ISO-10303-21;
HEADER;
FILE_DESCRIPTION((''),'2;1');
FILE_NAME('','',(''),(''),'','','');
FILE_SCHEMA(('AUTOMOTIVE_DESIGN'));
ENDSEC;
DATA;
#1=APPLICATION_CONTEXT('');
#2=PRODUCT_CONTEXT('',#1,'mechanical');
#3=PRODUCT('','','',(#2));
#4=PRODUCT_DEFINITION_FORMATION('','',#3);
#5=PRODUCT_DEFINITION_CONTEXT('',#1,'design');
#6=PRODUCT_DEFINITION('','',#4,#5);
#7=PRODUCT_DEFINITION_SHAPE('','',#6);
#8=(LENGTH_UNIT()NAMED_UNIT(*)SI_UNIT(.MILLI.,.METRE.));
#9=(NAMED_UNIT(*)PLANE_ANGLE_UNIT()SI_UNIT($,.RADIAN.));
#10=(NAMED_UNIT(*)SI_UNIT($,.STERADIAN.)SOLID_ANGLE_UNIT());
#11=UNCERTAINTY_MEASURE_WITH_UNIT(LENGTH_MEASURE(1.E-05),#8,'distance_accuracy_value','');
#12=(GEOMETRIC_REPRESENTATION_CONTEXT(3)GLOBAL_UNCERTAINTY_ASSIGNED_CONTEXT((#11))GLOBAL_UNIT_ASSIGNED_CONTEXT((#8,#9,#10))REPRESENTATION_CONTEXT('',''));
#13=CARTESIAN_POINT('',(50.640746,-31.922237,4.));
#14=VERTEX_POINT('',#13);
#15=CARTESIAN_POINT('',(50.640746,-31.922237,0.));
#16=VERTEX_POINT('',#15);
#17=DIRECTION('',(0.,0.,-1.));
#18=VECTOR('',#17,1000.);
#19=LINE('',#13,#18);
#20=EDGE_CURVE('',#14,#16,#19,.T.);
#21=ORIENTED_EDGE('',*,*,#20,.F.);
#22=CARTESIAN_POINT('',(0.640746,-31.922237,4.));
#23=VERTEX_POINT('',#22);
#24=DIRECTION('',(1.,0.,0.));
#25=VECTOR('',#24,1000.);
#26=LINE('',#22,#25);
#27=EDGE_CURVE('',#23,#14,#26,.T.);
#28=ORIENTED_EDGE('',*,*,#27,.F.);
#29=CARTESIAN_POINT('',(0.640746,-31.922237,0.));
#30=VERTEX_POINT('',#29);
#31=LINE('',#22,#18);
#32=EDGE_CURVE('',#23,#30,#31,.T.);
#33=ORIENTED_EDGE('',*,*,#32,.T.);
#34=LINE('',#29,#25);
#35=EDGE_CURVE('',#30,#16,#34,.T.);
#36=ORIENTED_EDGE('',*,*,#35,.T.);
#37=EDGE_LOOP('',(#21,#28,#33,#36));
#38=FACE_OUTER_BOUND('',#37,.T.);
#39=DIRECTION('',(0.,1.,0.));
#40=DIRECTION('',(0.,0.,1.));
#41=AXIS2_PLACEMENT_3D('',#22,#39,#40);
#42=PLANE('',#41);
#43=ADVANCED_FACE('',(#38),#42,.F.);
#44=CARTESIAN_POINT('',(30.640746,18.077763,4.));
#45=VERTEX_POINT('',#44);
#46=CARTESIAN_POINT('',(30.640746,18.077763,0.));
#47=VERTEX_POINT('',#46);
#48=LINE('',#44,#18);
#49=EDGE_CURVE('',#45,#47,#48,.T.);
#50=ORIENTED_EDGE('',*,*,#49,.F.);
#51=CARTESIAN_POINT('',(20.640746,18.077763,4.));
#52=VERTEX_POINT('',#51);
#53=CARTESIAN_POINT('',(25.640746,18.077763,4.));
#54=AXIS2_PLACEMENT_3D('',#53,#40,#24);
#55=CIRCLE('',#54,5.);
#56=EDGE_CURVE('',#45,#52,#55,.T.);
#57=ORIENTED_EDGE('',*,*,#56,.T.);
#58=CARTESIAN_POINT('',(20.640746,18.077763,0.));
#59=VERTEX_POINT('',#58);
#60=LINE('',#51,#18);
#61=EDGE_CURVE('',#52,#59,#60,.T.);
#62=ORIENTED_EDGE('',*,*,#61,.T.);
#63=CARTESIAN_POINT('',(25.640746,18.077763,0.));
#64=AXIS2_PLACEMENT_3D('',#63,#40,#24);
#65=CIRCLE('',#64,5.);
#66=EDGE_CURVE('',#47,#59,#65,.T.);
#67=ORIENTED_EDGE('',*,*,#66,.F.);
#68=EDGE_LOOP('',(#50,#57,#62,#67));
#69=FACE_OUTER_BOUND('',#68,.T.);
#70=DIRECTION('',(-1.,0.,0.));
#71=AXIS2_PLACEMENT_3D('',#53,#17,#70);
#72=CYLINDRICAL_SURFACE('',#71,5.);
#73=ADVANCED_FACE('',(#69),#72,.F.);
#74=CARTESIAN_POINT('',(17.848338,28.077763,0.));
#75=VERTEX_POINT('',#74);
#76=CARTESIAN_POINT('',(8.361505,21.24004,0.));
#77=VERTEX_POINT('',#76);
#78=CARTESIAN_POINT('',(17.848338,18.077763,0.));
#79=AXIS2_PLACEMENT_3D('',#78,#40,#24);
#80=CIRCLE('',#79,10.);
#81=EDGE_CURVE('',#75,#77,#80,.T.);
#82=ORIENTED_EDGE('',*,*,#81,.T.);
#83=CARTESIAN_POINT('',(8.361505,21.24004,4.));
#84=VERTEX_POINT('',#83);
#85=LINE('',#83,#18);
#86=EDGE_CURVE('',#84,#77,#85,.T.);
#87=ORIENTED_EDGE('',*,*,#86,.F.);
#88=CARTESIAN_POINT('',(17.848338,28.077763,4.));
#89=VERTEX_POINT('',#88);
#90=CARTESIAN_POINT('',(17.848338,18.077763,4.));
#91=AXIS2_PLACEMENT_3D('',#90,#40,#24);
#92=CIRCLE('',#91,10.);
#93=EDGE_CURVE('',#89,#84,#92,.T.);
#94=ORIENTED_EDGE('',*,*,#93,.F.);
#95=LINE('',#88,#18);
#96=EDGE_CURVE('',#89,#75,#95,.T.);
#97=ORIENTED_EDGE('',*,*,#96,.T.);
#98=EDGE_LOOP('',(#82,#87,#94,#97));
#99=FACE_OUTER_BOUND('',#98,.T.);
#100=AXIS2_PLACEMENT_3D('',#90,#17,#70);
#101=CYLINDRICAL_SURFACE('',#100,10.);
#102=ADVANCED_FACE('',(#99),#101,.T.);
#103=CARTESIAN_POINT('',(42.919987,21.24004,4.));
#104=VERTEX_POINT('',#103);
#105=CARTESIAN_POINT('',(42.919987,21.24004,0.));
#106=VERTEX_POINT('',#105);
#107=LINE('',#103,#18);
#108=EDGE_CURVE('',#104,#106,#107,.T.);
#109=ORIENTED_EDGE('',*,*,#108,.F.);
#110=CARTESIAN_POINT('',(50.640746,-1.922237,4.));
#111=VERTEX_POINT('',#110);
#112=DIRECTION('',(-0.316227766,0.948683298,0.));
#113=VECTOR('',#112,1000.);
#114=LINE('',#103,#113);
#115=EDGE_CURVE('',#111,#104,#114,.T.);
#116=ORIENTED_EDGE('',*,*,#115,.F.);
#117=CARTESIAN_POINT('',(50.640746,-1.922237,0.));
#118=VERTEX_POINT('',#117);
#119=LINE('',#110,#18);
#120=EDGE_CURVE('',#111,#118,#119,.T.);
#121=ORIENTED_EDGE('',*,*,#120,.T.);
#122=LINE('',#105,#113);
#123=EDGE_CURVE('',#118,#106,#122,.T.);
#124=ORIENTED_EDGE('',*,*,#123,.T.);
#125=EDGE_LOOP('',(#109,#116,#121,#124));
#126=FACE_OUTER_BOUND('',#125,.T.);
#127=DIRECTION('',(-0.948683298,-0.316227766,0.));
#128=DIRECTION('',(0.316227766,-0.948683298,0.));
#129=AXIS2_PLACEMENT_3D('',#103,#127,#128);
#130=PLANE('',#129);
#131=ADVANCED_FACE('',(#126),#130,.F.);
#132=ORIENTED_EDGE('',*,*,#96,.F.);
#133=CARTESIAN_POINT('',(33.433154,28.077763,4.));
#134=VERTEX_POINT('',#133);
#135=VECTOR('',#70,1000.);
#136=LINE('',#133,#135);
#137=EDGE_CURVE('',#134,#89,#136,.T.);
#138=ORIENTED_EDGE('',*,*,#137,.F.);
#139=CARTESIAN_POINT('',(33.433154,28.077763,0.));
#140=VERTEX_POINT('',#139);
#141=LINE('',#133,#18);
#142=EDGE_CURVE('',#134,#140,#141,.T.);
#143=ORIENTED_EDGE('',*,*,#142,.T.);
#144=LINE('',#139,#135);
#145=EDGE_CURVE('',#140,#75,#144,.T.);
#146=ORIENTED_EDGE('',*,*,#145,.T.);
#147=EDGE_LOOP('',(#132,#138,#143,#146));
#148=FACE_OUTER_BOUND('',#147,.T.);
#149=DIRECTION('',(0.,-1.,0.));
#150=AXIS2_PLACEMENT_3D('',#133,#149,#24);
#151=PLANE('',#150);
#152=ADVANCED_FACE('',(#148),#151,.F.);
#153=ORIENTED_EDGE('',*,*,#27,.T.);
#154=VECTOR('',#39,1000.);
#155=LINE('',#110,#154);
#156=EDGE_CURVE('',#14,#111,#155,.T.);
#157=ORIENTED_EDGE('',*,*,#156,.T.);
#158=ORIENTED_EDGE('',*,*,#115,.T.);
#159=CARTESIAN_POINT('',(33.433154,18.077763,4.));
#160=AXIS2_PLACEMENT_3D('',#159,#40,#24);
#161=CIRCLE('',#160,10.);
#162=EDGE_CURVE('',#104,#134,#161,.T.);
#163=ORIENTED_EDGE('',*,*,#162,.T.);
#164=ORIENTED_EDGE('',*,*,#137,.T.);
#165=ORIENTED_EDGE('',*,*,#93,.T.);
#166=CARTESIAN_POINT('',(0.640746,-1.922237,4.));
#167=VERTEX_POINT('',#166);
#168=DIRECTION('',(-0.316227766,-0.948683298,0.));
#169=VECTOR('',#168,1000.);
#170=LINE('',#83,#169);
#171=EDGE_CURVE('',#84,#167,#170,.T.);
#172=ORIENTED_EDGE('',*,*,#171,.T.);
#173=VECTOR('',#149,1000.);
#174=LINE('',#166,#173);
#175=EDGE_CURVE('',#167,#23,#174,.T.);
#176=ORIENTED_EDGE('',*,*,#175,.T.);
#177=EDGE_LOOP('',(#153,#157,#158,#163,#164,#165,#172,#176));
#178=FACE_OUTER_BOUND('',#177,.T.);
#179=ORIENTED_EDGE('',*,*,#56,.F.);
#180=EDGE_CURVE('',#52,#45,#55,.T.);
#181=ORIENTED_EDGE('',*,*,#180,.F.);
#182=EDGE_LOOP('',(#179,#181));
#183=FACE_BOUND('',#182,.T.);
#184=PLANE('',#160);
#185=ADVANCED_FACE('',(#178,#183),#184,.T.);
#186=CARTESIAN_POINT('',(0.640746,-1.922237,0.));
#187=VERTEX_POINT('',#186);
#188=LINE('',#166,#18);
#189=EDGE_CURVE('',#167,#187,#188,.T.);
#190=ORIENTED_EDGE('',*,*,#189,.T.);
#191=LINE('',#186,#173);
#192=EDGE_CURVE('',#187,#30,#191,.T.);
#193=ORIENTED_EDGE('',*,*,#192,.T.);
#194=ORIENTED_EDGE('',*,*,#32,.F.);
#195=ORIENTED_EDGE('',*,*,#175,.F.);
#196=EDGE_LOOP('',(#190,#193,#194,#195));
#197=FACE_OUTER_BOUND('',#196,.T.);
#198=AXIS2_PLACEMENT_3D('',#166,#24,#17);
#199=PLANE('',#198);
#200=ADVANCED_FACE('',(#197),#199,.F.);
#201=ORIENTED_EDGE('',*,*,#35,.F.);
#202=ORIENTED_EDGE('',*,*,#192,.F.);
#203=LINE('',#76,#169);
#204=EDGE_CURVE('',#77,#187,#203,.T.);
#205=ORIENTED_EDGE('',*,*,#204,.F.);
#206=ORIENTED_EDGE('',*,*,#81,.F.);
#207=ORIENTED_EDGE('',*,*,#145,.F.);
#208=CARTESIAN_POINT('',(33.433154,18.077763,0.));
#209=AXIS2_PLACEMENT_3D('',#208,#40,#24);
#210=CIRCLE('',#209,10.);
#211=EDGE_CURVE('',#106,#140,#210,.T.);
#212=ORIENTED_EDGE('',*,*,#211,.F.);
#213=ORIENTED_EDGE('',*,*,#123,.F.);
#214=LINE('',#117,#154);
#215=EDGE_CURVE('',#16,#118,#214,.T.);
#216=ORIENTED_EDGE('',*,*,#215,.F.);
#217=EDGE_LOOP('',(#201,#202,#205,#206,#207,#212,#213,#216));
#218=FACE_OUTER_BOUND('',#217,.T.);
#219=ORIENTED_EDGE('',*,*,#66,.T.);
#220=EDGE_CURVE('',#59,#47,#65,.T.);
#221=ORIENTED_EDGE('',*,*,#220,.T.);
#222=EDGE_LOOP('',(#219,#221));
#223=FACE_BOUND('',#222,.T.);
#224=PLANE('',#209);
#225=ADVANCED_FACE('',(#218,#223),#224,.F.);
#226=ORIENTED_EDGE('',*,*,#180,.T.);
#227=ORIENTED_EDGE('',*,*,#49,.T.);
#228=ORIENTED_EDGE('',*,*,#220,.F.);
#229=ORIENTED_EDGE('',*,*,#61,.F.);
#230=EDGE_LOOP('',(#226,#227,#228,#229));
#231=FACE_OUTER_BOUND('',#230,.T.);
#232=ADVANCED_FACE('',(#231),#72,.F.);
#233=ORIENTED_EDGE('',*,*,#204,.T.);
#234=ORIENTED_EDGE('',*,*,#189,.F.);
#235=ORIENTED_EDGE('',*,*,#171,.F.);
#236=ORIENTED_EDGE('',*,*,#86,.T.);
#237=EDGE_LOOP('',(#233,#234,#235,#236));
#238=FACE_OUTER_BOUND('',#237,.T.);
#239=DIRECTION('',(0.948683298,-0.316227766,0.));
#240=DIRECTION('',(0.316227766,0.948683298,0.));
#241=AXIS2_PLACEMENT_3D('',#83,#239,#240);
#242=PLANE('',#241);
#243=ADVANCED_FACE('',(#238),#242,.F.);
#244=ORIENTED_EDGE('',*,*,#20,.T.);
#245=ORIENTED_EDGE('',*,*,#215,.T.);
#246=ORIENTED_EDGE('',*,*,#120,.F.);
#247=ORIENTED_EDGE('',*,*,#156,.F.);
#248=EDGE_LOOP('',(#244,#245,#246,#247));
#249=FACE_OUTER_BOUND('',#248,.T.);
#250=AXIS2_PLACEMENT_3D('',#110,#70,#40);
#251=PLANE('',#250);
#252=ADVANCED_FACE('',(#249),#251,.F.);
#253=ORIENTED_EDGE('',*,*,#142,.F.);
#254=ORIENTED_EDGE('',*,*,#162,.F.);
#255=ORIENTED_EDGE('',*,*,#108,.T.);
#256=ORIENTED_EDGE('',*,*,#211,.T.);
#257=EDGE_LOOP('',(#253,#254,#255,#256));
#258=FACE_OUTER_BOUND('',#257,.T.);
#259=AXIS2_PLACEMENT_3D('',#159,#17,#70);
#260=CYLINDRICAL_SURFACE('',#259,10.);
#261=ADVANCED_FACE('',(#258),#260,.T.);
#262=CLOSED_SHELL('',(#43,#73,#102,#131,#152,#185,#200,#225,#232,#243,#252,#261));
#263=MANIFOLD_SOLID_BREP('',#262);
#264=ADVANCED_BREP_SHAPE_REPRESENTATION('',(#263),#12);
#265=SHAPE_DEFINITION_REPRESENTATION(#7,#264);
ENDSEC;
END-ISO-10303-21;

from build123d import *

# Parameters (mm, degrees)
SKETCH1_R           = 5
BOSS_EXTRUDE1_DEPTH = 4


with BuildPart() as part:
    # Sketch1 → Boss-Extrude1 (new body)
    with BuildSketch(Plane.XY):
        with BuildLine():
            Line((33.433153565, 28.077762704), (17.848337966, 28.077762704))
            ThreePointArc((17.848337966, 28.077762704), (12.001235119, 26.190184555), (8.361504986, 21.240040364))
            Line((8.361504986, 21.240040364), (0.640745765, -1.922237296))
            Line((0.640745765, -1.922237296), (0.640745765, -31.922237296))
            Line((0.640745765, -31.922237296), (50.640745765, -31.922237296))
            Line((50.640745765, -31.922237296), (50.640745765, -1.922237296))
            Line((50.640745765, -1.922237296), (42.919986545, 21.240040364))
            ThreePointArc((42.919986545, 21.240040364), (39.280256412, 26.190184555), (33.433153565, 28.077762704))
        make_face()
        with Locations((25.640745765, 18.077762704)):
            Circle(SKETCH1_R, mode=Mode.SUBTRACT)
    extrude(amount=BOSS_EXTRUDE1_DEPTH)


solid = part.part
